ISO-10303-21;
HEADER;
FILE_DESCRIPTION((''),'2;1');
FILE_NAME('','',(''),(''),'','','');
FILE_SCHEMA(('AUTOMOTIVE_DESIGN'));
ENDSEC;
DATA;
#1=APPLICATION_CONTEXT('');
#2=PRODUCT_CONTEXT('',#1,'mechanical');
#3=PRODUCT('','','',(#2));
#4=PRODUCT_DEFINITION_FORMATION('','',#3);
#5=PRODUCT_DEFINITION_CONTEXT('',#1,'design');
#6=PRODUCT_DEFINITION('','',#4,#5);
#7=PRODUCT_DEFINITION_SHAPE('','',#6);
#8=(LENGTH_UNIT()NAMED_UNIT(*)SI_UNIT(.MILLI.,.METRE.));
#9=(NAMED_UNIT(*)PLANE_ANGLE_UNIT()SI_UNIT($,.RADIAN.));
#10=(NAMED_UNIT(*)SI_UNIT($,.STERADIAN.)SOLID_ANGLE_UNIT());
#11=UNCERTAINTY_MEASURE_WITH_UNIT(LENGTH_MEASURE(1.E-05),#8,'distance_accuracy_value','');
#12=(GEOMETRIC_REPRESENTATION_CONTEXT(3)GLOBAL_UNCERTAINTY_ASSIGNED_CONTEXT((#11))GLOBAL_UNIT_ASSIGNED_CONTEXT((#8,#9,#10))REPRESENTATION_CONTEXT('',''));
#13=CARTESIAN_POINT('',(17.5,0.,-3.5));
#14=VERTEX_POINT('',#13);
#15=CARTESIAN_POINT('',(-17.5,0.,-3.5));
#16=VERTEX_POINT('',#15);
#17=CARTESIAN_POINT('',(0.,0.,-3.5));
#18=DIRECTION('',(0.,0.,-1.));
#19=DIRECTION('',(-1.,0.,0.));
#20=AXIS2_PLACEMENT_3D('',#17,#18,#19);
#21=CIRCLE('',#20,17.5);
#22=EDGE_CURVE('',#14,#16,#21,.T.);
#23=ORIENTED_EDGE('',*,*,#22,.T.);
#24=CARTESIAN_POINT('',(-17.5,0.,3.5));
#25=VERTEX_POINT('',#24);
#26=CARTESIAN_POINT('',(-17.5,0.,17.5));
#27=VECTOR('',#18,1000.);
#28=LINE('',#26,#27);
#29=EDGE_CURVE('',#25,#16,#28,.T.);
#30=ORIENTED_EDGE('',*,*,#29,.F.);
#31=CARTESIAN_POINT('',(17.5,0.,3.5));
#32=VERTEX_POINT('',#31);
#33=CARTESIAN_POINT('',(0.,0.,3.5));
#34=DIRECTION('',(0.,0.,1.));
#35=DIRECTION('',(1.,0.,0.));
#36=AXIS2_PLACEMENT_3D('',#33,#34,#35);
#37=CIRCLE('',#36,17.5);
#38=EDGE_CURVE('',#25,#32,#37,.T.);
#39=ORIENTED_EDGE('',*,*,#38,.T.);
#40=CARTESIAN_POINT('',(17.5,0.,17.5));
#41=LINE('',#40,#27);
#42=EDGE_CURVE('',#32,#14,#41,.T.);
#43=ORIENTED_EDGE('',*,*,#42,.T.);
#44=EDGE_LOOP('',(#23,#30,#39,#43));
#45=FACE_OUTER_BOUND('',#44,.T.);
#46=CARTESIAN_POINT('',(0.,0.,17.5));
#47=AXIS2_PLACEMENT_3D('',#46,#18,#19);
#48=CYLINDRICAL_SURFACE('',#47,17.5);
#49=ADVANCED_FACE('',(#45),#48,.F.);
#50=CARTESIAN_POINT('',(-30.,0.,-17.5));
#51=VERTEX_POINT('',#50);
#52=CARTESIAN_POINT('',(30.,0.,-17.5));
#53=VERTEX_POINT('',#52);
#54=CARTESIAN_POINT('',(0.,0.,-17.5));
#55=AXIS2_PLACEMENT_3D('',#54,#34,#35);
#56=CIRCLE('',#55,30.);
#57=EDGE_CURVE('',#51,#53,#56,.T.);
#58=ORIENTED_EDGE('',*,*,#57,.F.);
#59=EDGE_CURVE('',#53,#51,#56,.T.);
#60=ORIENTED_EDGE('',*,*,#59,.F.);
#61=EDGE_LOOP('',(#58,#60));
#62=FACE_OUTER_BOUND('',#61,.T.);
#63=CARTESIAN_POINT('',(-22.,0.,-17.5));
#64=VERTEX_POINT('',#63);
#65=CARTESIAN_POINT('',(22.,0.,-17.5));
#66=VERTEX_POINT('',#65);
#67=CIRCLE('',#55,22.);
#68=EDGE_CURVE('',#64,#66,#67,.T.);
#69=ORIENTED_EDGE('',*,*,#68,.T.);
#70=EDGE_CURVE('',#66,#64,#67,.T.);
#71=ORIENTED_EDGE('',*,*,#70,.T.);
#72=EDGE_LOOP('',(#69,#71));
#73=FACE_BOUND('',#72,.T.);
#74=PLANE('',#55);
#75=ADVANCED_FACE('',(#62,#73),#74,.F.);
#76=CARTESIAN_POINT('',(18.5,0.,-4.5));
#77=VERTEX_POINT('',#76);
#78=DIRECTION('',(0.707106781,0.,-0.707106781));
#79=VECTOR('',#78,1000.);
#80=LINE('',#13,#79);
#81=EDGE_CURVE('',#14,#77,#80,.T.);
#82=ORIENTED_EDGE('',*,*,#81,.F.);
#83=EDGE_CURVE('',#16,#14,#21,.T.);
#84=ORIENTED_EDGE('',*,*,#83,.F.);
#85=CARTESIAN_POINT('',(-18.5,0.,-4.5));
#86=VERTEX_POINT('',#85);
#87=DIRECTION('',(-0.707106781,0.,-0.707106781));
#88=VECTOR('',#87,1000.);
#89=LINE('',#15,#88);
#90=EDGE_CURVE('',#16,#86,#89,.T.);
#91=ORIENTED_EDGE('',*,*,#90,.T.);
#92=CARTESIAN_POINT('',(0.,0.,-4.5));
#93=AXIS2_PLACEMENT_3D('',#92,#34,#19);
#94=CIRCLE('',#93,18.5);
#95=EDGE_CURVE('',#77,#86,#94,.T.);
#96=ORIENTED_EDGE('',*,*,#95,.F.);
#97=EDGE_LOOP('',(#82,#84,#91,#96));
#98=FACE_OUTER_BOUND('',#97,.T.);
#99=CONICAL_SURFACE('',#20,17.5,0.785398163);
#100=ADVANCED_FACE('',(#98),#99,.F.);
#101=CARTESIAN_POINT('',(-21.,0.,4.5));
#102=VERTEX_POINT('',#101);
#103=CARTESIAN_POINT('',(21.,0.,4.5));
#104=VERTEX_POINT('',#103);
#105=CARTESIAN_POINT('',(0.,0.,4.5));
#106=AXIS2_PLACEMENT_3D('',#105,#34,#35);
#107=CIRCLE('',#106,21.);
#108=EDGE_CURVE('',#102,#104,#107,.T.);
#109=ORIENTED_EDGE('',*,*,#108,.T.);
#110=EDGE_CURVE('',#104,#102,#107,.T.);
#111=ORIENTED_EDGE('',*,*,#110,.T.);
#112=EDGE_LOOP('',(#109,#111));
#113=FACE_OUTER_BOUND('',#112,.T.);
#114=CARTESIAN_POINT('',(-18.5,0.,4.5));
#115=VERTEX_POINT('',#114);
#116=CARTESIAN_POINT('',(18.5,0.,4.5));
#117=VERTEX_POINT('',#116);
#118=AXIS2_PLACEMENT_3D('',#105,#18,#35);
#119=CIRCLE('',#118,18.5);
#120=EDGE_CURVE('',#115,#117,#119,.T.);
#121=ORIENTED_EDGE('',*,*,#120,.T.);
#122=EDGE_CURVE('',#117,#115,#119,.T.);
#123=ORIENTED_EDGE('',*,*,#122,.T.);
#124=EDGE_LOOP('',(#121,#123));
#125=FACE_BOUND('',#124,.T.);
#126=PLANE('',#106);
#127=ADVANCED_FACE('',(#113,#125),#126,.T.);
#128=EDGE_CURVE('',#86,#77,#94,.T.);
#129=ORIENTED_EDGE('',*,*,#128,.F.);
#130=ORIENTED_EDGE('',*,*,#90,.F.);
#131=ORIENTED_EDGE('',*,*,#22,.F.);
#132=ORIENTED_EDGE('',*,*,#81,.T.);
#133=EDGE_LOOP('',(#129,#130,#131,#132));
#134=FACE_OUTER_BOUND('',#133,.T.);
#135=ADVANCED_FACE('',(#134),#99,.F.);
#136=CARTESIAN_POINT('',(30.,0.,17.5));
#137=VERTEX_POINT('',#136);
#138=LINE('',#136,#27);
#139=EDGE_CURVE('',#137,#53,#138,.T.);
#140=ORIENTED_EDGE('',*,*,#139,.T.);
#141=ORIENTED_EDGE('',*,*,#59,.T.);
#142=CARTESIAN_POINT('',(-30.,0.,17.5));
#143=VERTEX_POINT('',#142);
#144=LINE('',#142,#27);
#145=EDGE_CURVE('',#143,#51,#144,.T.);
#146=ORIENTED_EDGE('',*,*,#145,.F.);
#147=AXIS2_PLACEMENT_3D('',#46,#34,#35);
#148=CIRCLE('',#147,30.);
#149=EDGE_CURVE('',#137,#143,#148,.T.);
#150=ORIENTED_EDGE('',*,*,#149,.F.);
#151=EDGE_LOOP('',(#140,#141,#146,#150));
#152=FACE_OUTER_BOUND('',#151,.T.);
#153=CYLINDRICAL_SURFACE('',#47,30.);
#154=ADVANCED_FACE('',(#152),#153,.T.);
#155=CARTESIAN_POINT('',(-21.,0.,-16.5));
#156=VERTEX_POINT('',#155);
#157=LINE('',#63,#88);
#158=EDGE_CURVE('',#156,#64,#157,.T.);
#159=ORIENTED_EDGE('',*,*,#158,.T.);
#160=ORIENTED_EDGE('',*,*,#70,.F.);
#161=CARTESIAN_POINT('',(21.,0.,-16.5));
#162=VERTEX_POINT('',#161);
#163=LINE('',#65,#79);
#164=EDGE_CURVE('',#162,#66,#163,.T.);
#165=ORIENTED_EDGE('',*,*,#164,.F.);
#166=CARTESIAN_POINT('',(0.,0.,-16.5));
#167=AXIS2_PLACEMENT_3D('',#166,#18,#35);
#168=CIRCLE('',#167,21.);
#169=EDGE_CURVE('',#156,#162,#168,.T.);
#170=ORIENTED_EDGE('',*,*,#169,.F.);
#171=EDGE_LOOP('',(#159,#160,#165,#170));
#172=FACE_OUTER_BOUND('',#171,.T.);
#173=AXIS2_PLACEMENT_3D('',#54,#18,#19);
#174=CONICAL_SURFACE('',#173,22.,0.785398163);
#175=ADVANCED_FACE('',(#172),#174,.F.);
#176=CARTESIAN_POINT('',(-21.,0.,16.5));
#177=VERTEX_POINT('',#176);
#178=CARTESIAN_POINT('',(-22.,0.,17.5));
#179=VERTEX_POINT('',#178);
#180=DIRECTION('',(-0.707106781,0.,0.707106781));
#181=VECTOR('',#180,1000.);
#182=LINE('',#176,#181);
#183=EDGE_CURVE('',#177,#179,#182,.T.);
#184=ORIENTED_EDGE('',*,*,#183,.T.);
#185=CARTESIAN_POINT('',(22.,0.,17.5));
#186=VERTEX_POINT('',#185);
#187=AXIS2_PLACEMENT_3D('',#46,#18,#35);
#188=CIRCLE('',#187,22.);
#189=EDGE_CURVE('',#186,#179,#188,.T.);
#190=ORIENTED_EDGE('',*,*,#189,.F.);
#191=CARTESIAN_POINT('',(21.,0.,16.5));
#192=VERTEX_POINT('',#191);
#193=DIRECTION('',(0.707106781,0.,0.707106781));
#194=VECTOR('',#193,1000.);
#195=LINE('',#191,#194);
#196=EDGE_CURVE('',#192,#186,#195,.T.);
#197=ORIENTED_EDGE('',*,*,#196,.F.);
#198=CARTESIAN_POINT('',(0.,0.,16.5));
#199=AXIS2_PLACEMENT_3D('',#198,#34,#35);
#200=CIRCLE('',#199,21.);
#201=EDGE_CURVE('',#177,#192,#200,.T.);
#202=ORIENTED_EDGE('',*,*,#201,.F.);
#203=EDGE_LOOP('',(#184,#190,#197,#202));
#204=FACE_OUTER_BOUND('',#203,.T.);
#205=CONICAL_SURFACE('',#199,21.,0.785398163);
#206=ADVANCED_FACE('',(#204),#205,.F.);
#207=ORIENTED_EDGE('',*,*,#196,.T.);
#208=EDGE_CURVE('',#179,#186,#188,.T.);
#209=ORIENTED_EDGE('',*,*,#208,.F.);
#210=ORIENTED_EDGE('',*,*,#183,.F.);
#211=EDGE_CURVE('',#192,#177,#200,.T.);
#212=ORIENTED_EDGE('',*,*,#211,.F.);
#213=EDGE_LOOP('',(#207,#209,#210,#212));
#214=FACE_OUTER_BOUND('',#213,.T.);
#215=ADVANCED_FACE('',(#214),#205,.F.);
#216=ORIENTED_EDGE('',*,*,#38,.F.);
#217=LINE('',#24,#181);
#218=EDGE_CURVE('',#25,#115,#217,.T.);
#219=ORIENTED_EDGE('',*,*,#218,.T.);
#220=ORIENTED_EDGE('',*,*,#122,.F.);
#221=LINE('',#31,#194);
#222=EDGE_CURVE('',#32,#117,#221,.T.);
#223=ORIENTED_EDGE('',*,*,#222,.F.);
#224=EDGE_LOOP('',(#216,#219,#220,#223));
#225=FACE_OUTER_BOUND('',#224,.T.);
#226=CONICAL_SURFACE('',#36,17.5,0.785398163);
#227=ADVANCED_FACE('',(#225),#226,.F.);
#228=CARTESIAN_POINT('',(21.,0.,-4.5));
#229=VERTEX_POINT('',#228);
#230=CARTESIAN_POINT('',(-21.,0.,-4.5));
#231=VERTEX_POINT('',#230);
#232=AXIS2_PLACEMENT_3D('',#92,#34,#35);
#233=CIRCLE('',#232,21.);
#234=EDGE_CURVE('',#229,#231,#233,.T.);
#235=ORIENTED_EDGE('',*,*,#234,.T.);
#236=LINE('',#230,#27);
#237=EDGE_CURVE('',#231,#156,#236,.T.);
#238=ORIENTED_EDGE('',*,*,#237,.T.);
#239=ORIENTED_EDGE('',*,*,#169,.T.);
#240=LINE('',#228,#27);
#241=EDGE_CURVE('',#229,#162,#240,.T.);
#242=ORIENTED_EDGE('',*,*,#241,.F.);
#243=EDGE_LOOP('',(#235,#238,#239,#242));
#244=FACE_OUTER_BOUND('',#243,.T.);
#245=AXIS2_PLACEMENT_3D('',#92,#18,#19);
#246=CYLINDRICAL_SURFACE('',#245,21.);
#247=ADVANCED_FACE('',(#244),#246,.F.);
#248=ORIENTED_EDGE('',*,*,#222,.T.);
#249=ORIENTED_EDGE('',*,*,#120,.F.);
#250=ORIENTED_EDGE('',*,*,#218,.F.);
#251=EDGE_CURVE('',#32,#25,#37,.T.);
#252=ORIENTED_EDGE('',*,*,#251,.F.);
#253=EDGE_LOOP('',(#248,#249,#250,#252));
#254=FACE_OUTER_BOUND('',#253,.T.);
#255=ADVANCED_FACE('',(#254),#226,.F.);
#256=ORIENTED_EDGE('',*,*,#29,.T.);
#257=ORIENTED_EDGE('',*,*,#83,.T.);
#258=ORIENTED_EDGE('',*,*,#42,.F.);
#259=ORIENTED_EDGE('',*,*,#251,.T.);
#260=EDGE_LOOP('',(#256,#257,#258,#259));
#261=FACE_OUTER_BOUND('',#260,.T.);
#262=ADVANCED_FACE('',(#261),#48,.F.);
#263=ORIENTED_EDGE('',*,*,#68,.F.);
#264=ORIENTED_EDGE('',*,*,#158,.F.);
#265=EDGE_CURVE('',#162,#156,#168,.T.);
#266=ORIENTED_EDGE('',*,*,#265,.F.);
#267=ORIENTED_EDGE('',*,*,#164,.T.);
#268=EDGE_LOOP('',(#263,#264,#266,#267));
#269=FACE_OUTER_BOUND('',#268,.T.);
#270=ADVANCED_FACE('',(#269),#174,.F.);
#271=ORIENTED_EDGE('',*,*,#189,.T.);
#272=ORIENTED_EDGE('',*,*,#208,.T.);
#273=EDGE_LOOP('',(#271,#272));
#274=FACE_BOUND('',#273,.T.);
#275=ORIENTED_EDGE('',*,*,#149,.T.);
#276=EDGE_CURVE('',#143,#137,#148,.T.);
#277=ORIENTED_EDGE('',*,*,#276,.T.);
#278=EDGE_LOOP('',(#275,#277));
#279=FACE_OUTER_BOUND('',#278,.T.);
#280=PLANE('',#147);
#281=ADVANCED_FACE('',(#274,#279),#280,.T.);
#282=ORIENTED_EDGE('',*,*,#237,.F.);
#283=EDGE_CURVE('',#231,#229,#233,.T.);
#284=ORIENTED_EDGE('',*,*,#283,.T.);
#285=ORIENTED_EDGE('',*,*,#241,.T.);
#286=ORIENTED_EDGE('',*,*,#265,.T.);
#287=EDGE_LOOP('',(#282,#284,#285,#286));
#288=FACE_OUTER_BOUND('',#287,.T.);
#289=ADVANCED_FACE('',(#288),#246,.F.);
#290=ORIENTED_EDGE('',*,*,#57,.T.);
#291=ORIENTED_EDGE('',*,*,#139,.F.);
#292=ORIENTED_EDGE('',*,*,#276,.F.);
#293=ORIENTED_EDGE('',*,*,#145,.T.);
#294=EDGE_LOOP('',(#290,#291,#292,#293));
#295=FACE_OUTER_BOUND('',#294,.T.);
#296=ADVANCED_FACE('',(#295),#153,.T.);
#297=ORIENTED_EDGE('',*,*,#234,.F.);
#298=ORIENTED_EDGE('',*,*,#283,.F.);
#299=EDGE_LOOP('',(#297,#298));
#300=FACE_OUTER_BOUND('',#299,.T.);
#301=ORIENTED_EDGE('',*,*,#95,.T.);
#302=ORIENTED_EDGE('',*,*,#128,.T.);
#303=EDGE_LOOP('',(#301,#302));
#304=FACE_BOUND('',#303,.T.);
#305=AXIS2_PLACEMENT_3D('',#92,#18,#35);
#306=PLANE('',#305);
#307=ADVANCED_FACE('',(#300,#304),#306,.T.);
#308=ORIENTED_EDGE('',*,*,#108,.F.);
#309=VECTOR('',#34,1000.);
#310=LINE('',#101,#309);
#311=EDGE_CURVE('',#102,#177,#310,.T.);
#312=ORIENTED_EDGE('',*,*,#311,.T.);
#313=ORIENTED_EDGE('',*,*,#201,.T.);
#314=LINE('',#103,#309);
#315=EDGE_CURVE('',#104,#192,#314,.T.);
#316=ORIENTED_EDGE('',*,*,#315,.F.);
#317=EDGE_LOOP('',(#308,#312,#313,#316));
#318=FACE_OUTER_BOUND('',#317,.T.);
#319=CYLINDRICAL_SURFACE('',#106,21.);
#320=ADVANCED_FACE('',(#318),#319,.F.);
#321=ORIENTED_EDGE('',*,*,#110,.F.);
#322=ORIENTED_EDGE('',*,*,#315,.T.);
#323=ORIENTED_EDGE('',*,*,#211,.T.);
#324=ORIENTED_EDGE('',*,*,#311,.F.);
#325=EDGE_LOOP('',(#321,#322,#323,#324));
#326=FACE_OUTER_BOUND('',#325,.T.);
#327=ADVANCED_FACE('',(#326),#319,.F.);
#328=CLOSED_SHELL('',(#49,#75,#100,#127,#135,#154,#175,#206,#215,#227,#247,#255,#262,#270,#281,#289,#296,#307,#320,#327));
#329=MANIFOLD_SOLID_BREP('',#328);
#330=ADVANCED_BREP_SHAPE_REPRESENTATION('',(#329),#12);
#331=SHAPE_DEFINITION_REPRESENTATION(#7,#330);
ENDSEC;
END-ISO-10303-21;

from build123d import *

# Parameters (mm, degrees)
SKETCH_1_R          = 30
SKETCH_1_R_2        = 17.5
EXTRUDE_1_DEPTH     = 17.5
SKETCH_2_R          = 21
CUT_EXTRUDE_1_DEPTH = 13
CHAMFER_1_SIZE      = 1


with BuildPart() as part:
    # 草图1 → 凸台-拉伸1 (new, symmetric)
    with BuildSketch(Plane.XY):
        Circle(SKETCH_1_R)
        Circle(SKETCH_1_R_2, mode=Mode.SUBTRACT)
    extrude(amount=EXTRUDE_1_DEPTH, both=True)

    # 草图2 → 切除-拉伸1 (cut)
    with BuildSketch(Plane.XY.offset(17.5)):
        Circle(SKETCH_2_R)
    cut_extrude_1 = extrude(amount=-CUT_EXTRUDE_1_DEPTH, mode=Mode.SUBTRACT)

    # 镜向1: 切除-拉伸1 across plane
    add(cut_extrude_1.mirror(Plane.XY), mode=Mode.SUBTRACT)

    # 倒角1
    chamfer_1_edges = [part.edges().sort_by_distance(p)[0] for p in [
        (-17.5, 0, 4.5),
        (-21, 0, 17.5),
        (-21, 0, -17.5),
        (-17.5, 0, -4.5),
    ]]
    chamfer(chamfer_1_edges, length=CHAMFER_1_SIZE)


solid = part.part
